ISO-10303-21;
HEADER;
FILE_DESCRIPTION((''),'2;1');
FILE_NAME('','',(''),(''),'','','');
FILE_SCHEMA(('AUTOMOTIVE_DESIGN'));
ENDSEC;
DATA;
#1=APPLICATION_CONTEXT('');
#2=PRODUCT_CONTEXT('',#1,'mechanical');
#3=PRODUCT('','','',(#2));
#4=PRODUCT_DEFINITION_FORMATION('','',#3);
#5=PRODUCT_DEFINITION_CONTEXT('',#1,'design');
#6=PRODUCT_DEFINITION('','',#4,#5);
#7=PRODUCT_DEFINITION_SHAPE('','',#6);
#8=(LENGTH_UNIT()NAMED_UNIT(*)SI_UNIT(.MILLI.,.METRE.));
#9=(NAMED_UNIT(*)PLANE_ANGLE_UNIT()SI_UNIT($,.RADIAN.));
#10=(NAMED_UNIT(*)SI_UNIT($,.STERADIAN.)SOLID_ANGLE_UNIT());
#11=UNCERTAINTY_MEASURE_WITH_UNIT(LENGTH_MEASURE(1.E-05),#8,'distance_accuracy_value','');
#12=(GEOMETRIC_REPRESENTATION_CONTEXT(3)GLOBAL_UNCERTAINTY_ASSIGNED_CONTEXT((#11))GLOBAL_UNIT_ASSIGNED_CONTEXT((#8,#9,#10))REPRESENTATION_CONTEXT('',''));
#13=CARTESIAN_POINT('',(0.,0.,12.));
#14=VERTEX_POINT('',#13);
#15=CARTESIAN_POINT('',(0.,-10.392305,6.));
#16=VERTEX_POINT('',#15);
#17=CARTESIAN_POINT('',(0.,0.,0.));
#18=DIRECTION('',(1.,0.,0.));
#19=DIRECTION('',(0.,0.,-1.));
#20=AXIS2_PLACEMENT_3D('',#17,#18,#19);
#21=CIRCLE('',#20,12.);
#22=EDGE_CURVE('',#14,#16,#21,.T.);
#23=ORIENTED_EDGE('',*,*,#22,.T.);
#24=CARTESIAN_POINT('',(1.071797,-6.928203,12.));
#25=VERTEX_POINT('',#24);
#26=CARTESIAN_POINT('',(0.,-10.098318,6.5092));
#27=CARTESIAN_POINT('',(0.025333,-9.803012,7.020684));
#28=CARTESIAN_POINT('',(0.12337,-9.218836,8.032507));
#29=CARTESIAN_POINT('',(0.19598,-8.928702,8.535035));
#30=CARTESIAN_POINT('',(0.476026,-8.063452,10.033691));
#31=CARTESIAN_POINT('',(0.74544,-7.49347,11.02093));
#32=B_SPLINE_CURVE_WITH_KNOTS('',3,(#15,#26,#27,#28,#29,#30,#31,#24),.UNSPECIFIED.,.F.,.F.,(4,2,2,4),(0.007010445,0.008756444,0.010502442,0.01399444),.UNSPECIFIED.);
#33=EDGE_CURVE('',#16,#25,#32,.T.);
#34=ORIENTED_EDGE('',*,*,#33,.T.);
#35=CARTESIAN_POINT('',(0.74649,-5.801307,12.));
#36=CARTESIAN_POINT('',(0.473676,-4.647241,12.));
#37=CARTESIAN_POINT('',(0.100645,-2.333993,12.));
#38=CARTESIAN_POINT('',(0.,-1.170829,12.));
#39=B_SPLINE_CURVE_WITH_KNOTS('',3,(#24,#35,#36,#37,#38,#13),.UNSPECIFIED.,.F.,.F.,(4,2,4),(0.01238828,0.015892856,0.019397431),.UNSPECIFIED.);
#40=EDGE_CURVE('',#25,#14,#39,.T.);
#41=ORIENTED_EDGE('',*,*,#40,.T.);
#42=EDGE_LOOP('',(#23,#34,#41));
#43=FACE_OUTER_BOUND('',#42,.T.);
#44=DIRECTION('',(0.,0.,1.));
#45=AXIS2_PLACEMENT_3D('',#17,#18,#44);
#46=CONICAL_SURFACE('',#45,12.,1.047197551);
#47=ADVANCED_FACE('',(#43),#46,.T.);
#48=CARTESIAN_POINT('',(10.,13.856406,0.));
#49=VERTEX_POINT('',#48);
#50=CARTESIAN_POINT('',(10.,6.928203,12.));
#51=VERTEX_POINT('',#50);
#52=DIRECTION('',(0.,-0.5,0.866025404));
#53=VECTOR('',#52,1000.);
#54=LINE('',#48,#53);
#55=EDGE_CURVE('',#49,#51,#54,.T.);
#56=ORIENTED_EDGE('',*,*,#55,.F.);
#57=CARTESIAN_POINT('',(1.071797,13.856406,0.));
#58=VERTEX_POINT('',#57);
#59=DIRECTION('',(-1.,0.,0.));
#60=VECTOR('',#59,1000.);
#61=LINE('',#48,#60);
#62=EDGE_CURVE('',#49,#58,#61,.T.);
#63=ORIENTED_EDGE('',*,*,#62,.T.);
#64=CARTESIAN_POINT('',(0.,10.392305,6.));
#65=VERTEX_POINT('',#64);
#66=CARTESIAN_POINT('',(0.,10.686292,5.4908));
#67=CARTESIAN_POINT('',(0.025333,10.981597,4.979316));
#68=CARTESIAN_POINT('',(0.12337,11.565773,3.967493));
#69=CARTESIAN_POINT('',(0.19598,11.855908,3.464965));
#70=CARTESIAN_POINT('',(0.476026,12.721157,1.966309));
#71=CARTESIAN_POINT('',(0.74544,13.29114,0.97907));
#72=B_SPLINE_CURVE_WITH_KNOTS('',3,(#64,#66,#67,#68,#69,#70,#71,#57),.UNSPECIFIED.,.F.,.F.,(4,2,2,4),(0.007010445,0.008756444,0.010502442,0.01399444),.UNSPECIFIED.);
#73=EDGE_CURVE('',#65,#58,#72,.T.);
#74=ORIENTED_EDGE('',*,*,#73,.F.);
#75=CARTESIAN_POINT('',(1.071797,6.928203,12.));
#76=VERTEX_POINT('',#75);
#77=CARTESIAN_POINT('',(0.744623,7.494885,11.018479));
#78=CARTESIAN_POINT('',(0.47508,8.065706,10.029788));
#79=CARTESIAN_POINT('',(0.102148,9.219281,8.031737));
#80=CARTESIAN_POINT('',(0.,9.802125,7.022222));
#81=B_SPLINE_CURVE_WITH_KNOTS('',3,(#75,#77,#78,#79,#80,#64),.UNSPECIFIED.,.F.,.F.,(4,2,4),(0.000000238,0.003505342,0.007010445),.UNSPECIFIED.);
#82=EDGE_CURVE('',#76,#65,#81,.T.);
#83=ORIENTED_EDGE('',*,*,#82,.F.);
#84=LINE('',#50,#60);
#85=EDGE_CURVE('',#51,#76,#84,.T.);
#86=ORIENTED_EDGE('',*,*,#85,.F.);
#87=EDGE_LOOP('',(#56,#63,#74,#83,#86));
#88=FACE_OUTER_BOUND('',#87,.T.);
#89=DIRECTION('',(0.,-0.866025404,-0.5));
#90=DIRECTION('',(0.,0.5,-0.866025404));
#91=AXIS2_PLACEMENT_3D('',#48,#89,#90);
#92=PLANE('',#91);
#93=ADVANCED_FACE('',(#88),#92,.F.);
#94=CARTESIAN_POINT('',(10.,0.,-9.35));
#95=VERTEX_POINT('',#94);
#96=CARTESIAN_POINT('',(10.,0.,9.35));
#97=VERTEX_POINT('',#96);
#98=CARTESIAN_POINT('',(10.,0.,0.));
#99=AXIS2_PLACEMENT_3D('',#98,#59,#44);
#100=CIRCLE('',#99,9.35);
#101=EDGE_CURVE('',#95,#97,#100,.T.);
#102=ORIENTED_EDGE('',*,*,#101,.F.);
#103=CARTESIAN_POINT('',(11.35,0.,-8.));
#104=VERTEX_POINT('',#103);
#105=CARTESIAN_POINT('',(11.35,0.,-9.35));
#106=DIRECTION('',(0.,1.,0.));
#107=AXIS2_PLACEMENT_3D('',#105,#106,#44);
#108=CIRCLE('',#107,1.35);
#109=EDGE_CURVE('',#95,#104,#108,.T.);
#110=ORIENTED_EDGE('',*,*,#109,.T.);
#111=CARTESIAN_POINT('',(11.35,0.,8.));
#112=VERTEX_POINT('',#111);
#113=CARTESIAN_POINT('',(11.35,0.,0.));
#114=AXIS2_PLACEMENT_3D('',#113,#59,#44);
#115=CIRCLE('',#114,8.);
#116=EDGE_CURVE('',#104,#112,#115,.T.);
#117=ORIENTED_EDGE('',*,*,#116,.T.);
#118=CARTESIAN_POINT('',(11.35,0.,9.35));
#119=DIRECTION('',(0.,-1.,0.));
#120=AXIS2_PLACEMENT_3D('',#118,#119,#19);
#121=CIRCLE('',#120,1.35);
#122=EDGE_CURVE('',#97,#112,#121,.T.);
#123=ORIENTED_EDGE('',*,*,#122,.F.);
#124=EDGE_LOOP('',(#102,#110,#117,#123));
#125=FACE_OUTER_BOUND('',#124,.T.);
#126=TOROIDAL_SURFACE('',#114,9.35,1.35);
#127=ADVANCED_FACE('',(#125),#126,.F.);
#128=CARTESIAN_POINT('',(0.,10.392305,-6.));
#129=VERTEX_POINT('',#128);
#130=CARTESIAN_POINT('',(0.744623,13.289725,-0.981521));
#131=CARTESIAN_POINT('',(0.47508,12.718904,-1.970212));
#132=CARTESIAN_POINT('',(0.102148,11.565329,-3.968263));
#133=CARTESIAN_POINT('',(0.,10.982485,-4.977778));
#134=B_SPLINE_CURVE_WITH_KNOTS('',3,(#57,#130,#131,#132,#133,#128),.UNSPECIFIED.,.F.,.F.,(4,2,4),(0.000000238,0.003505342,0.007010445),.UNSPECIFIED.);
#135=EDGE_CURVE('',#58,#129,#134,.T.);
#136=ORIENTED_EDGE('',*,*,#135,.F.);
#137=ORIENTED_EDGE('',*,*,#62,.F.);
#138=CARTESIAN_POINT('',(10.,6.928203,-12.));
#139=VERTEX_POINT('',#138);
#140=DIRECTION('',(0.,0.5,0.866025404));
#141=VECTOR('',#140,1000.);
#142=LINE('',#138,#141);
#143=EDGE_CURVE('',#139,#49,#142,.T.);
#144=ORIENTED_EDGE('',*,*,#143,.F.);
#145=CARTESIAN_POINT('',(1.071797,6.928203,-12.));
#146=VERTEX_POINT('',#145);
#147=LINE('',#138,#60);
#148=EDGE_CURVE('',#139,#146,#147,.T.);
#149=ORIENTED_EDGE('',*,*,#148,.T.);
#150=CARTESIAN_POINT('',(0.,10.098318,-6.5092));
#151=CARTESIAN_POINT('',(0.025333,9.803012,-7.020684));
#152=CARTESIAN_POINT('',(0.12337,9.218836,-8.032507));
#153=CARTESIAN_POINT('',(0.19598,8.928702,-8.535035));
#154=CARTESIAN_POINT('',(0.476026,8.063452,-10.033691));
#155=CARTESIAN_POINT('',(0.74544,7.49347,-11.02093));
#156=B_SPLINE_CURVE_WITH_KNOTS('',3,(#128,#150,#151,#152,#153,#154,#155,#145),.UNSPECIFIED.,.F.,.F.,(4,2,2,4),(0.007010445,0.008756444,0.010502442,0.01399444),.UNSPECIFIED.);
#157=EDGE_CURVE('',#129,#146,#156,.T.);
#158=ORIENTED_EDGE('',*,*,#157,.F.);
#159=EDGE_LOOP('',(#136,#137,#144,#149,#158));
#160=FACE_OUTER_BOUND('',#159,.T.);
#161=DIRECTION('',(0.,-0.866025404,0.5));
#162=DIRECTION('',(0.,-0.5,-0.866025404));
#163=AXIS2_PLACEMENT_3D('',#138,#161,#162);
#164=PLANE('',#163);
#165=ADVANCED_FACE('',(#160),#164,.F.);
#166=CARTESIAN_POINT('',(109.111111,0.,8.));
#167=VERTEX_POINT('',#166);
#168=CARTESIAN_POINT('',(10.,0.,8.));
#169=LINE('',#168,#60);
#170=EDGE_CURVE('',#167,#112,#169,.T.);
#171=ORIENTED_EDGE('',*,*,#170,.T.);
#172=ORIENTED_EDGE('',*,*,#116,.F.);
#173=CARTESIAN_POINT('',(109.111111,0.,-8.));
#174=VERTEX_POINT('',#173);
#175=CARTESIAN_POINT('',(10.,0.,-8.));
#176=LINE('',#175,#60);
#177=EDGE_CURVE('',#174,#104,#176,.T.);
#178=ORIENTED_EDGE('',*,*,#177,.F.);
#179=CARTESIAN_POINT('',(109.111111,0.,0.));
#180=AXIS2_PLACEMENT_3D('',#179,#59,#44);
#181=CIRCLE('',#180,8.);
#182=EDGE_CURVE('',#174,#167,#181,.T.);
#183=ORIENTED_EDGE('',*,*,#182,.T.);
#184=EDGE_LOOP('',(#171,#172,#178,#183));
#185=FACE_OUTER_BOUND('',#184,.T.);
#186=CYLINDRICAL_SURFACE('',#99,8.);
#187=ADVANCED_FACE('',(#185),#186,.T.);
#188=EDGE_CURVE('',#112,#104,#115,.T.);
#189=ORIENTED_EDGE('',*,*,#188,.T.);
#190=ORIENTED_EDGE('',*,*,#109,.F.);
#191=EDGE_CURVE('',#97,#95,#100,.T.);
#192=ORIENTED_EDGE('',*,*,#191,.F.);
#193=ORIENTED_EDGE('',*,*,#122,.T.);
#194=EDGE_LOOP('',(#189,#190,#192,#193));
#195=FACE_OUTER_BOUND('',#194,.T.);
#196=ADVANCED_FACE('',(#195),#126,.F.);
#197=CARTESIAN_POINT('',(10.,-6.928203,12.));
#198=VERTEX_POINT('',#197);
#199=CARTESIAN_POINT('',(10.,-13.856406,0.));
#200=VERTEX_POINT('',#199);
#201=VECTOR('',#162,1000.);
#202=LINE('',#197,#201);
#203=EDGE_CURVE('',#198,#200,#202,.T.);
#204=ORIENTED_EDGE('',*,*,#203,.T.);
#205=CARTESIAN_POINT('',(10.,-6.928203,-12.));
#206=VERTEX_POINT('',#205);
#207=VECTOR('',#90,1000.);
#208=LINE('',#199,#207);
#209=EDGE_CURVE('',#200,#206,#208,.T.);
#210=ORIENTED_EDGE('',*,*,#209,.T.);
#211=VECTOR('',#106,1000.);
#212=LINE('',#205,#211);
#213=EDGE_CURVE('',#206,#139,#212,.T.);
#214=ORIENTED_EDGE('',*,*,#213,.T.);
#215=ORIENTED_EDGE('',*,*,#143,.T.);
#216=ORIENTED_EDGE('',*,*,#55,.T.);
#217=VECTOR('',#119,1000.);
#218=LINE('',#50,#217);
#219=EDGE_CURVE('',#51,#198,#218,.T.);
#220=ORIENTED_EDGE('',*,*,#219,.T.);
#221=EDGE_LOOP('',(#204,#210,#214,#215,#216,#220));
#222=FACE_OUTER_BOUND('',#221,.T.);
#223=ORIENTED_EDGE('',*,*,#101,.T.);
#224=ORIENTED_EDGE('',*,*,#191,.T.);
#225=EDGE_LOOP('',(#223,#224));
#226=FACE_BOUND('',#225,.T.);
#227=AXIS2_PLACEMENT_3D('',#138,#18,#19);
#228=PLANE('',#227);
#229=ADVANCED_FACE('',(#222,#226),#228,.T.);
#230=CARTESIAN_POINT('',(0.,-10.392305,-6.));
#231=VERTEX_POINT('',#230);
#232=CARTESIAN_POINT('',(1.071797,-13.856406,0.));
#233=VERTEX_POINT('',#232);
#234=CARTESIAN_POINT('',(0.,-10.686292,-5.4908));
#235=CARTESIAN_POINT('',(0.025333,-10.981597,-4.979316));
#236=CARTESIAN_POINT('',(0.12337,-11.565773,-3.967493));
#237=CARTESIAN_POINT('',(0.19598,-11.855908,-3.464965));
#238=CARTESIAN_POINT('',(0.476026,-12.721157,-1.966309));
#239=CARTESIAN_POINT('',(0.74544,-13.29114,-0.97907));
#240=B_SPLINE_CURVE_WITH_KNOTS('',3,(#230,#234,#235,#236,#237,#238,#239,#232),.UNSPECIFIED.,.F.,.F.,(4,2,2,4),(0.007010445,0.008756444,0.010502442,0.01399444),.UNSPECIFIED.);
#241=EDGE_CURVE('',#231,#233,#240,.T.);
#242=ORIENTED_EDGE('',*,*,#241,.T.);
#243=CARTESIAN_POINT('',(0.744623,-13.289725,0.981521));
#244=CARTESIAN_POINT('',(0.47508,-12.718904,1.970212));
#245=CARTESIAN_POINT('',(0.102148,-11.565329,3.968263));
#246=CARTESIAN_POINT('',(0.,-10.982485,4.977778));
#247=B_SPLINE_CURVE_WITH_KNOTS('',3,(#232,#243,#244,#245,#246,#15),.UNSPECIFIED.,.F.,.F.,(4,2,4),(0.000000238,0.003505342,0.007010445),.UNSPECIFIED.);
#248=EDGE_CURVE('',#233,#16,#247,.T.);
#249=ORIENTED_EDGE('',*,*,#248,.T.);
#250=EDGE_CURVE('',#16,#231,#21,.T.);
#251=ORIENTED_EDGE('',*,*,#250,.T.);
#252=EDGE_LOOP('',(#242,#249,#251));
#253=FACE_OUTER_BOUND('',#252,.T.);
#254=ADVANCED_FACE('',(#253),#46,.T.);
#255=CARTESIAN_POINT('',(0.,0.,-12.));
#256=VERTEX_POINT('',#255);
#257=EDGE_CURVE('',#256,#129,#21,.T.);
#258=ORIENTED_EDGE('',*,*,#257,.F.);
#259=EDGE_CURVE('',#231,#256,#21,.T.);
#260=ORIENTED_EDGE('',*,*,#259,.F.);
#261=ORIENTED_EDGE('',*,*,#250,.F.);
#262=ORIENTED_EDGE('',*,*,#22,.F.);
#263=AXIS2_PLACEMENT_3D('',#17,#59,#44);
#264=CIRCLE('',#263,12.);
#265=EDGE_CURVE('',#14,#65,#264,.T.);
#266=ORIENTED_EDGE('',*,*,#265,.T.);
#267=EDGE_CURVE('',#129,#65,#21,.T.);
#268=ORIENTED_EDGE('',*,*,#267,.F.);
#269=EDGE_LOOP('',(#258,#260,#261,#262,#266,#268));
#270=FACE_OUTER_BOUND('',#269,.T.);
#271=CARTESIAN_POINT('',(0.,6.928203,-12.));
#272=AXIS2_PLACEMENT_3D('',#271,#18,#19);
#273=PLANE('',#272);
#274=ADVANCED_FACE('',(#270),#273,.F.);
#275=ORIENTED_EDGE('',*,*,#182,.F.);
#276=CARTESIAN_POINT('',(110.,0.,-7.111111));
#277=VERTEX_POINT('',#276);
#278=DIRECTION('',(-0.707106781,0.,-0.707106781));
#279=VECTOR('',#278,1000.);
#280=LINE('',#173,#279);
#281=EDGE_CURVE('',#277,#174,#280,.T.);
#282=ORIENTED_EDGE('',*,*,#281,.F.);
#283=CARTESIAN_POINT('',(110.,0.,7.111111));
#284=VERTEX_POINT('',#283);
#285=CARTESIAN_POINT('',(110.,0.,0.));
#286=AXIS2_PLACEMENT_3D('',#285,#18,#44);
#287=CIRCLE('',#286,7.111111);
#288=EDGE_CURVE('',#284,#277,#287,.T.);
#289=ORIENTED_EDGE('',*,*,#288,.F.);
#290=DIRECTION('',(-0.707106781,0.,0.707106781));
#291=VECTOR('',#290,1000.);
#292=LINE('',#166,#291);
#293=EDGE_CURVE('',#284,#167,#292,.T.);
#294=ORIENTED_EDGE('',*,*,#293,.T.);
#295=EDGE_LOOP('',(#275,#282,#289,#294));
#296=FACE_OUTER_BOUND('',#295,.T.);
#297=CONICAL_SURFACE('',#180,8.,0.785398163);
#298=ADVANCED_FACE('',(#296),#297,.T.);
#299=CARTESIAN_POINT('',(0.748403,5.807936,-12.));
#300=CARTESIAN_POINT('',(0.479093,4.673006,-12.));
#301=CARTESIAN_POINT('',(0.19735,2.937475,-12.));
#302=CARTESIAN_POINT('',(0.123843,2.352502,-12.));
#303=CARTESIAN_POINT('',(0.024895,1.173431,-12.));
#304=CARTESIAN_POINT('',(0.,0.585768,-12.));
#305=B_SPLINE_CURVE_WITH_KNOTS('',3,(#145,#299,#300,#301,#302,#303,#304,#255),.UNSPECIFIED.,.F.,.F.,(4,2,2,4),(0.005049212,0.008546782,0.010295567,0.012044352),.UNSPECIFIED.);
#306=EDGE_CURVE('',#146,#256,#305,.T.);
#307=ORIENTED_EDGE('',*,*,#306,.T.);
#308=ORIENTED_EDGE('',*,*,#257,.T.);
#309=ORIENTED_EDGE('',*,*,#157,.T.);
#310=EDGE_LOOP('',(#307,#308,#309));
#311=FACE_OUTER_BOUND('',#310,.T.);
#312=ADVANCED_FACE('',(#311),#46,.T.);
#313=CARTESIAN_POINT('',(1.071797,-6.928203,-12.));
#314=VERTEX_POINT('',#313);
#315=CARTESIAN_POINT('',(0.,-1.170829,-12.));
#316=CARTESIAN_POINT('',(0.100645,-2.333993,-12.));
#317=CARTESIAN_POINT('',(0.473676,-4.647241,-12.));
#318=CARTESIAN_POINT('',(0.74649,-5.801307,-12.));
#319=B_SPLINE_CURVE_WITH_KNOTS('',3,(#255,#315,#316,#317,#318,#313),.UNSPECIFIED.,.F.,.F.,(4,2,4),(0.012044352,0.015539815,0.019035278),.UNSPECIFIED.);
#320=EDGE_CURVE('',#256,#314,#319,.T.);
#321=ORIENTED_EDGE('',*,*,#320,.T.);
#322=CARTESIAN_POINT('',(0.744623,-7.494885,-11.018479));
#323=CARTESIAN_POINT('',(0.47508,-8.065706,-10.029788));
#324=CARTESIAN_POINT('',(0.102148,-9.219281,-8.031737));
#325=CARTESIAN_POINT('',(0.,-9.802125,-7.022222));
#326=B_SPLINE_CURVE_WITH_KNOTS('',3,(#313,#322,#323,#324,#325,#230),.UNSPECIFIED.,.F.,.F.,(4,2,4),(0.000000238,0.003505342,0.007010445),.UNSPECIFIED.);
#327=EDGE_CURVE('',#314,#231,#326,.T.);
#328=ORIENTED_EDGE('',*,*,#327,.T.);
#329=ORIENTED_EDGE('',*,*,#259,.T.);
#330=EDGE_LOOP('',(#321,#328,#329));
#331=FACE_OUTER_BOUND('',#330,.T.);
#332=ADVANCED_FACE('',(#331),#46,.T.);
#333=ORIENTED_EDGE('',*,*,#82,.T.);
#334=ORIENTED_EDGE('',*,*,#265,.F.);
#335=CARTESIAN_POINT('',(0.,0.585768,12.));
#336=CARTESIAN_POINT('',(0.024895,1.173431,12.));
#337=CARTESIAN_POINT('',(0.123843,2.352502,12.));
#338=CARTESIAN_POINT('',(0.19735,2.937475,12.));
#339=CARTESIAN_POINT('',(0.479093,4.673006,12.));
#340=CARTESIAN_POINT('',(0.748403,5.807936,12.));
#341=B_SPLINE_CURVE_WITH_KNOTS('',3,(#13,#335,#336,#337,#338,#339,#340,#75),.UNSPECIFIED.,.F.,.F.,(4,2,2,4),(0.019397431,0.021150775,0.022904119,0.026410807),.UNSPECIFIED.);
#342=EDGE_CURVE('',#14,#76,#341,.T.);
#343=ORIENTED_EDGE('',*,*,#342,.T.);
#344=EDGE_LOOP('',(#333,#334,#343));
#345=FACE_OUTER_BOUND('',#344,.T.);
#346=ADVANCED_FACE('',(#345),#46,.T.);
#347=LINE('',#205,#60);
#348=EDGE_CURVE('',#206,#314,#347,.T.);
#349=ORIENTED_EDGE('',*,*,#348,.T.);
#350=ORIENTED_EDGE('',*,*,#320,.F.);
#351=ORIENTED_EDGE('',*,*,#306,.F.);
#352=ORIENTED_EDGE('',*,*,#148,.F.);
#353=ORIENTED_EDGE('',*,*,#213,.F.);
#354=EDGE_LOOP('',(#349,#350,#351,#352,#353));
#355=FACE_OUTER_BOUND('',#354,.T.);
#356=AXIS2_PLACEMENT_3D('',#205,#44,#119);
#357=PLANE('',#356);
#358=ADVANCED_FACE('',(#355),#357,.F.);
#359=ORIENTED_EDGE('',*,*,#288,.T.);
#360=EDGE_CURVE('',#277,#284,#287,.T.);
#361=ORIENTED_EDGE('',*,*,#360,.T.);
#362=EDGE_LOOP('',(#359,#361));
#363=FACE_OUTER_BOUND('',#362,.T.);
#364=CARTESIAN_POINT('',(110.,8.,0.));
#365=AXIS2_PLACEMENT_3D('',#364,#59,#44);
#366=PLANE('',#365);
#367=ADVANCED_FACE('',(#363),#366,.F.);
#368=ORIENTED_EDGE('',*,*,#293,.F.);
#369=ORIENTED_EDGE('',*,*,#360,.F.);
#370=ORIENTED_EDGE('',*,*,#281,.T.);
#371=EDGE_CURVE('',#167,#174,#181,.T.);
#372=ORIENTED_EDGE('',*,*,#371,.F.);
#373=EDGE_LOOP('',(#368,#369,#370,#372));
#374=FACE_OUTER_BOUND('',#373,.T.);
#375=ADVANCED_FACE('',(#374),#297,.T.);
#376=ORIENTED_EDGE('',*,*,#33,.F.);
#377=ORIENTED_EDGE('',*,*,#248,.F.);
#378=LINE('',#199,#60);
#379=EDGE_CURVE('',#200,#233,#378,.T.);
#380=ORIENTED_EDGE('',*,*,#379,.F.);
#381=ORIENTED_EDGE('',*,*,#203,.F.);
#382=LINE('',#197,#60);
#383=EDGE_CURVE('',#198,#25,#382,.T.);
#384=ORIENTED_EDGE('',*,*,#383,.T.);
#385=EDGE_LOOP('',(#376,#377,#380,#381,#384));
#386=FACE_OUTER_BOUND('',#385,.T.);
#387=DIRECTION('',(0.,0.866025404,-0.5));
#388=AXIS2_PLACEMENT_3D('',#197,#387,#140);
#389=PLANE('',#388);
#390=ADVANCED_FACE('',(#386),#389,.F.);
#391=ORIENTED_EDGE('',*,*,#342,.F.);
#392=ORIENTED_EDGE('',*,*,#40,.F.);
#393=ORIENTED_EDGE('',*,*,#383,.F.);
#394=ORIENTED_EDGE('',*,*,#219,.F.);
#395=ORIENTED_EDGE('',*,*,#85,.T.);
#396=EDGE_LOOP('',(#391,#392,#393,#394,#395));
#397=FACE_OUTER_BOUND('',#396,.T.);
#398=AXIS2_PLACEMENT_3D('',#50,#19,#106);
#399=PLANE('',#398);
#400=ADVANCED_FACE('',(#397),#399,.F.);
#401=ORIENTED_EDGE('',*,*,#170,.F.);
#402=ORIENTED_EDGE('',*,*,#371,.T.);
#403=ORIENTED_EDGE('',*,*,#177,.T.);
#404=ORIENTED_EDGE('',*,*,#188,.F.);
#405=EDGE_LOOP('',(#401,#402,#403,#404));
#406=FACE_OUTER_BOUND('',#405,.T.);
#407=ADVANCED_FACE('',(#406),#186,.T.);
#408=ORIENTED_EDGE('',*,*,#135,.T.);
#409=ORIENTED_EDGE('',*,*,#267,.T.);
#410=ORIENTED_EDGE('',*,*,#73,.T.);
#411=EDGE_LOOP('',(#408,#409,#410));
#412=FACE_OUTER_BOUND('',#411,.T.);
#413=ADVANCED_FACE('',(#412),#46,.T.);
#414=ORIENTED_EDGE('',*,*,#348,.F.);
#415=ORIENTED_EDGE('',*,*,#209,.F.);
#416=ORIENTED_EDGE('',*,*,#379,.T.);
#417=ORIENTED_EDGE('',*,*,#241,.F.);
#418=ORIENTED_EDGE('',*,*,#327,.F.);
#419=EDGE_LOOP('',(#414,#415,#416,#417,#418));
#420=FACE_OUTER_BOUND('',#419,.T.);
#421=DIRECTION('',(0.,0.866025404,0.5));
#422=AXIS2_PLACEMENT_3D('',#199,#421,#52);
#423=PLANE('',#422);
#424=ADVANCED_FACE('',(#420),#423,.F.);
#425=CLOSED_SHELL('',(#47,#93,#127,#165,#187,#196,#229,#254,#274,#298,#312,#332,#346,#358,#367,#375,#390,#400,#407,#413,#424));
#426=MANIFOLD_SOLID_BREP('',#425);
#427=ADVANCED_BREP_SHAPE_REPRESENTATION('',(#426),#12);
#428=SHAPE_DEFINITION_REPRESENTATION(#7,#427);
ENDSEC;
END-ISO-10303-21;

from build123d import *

# Parameters (mm, degrees)
BOSS_EXTRUDE1_DEPTH = 10
SKETCH4_R           = 26.17
SKETCH4_R_2         = 12
CUT_EXTRUDE1_DEPTH  = 1.25
CUT_EXTRUDE1_DRAFT  = -60
CHAMFER2_SIZE       = 0.888888889


with BuildPart() as part:
    # Sketch3 → Boss-Extrude1 (new body)
    with BuildSketch(Plane(origin=(0, 0, 0), x_dir=(0, 0, -1), z_dir=(1, 0, 0))):
        Polygon((12, 6.92820323), (0, 13.856406461), (-12, 6.92820323), (-12, -6.92820323), (0, -13.856406461), (12, -6.92820323), align=None)
    extrude(amount=BOSS_EXTRUDE1_DEPTH)


with BuildPart() as cut_extrude1_tool:
    # Sketch4 → Cut-Extrude1 (with draft: the straight prism first)
    with BuildSketch(Plane.ZY):
        Circle(SKETCH4_R)
        Circle(SKETCH4_R_2, mode=Mode.SUBTRACT)
    extrude(amount=-CUT_EXTRUDE1_DEPTH)
    # Cut-Extrude1: the draft: its side faces are tilted about the plane it starts from
    cut_extrude1_sides = [cut_extrude1_tool.faces().sort_by_distance(p)[0] for p in [
        (0.625, 0, -26.17),
        (0.625, 0, -12),
    ]]
    draft(cut_extrude1_sides, Plane.ZY, CUT_EXTRUDE1_DRAFT)


with BuildPart() as part_1:
    add(part.part)

    # Cut-Extrude1: cut by cut_extrude1_tool
    add(cut_extrude1_tool.part, mode=Mode.SUBTRACT)

    # Sketch5 → Revolve1 (revolve)
    with BuildSketch(Plane.XY, mode=Mode.PRIVATE) as revolve1_sk:
        with BuildLine():
            Line((11.35, 8), (110, 8))
            Line((110, 8), (110, 0))
            Line((110, 0), (10, 0))
            Line((10, 0), (10, 9.35))
            ThreePointArc((10, 9.35), (10.395405845, 8.395405845), (11.35, 8))
        make_face()
    revolve(revolve1_sk.sketch.rotate(Axis((10, 0, 0), (1, 0, 0)), 90), axis=Axis((10, 0, 0), (1, 0, 0)))

    # Chamfer2
    chamfer2_edges = [part_1.edges().sort_by_distance(p)[0] for p in [
        (110, 0, -8),
    ]]
    chamfer(chamfer2_edges, length=CHAMFER2_SIZE)


solid = part_1.part
